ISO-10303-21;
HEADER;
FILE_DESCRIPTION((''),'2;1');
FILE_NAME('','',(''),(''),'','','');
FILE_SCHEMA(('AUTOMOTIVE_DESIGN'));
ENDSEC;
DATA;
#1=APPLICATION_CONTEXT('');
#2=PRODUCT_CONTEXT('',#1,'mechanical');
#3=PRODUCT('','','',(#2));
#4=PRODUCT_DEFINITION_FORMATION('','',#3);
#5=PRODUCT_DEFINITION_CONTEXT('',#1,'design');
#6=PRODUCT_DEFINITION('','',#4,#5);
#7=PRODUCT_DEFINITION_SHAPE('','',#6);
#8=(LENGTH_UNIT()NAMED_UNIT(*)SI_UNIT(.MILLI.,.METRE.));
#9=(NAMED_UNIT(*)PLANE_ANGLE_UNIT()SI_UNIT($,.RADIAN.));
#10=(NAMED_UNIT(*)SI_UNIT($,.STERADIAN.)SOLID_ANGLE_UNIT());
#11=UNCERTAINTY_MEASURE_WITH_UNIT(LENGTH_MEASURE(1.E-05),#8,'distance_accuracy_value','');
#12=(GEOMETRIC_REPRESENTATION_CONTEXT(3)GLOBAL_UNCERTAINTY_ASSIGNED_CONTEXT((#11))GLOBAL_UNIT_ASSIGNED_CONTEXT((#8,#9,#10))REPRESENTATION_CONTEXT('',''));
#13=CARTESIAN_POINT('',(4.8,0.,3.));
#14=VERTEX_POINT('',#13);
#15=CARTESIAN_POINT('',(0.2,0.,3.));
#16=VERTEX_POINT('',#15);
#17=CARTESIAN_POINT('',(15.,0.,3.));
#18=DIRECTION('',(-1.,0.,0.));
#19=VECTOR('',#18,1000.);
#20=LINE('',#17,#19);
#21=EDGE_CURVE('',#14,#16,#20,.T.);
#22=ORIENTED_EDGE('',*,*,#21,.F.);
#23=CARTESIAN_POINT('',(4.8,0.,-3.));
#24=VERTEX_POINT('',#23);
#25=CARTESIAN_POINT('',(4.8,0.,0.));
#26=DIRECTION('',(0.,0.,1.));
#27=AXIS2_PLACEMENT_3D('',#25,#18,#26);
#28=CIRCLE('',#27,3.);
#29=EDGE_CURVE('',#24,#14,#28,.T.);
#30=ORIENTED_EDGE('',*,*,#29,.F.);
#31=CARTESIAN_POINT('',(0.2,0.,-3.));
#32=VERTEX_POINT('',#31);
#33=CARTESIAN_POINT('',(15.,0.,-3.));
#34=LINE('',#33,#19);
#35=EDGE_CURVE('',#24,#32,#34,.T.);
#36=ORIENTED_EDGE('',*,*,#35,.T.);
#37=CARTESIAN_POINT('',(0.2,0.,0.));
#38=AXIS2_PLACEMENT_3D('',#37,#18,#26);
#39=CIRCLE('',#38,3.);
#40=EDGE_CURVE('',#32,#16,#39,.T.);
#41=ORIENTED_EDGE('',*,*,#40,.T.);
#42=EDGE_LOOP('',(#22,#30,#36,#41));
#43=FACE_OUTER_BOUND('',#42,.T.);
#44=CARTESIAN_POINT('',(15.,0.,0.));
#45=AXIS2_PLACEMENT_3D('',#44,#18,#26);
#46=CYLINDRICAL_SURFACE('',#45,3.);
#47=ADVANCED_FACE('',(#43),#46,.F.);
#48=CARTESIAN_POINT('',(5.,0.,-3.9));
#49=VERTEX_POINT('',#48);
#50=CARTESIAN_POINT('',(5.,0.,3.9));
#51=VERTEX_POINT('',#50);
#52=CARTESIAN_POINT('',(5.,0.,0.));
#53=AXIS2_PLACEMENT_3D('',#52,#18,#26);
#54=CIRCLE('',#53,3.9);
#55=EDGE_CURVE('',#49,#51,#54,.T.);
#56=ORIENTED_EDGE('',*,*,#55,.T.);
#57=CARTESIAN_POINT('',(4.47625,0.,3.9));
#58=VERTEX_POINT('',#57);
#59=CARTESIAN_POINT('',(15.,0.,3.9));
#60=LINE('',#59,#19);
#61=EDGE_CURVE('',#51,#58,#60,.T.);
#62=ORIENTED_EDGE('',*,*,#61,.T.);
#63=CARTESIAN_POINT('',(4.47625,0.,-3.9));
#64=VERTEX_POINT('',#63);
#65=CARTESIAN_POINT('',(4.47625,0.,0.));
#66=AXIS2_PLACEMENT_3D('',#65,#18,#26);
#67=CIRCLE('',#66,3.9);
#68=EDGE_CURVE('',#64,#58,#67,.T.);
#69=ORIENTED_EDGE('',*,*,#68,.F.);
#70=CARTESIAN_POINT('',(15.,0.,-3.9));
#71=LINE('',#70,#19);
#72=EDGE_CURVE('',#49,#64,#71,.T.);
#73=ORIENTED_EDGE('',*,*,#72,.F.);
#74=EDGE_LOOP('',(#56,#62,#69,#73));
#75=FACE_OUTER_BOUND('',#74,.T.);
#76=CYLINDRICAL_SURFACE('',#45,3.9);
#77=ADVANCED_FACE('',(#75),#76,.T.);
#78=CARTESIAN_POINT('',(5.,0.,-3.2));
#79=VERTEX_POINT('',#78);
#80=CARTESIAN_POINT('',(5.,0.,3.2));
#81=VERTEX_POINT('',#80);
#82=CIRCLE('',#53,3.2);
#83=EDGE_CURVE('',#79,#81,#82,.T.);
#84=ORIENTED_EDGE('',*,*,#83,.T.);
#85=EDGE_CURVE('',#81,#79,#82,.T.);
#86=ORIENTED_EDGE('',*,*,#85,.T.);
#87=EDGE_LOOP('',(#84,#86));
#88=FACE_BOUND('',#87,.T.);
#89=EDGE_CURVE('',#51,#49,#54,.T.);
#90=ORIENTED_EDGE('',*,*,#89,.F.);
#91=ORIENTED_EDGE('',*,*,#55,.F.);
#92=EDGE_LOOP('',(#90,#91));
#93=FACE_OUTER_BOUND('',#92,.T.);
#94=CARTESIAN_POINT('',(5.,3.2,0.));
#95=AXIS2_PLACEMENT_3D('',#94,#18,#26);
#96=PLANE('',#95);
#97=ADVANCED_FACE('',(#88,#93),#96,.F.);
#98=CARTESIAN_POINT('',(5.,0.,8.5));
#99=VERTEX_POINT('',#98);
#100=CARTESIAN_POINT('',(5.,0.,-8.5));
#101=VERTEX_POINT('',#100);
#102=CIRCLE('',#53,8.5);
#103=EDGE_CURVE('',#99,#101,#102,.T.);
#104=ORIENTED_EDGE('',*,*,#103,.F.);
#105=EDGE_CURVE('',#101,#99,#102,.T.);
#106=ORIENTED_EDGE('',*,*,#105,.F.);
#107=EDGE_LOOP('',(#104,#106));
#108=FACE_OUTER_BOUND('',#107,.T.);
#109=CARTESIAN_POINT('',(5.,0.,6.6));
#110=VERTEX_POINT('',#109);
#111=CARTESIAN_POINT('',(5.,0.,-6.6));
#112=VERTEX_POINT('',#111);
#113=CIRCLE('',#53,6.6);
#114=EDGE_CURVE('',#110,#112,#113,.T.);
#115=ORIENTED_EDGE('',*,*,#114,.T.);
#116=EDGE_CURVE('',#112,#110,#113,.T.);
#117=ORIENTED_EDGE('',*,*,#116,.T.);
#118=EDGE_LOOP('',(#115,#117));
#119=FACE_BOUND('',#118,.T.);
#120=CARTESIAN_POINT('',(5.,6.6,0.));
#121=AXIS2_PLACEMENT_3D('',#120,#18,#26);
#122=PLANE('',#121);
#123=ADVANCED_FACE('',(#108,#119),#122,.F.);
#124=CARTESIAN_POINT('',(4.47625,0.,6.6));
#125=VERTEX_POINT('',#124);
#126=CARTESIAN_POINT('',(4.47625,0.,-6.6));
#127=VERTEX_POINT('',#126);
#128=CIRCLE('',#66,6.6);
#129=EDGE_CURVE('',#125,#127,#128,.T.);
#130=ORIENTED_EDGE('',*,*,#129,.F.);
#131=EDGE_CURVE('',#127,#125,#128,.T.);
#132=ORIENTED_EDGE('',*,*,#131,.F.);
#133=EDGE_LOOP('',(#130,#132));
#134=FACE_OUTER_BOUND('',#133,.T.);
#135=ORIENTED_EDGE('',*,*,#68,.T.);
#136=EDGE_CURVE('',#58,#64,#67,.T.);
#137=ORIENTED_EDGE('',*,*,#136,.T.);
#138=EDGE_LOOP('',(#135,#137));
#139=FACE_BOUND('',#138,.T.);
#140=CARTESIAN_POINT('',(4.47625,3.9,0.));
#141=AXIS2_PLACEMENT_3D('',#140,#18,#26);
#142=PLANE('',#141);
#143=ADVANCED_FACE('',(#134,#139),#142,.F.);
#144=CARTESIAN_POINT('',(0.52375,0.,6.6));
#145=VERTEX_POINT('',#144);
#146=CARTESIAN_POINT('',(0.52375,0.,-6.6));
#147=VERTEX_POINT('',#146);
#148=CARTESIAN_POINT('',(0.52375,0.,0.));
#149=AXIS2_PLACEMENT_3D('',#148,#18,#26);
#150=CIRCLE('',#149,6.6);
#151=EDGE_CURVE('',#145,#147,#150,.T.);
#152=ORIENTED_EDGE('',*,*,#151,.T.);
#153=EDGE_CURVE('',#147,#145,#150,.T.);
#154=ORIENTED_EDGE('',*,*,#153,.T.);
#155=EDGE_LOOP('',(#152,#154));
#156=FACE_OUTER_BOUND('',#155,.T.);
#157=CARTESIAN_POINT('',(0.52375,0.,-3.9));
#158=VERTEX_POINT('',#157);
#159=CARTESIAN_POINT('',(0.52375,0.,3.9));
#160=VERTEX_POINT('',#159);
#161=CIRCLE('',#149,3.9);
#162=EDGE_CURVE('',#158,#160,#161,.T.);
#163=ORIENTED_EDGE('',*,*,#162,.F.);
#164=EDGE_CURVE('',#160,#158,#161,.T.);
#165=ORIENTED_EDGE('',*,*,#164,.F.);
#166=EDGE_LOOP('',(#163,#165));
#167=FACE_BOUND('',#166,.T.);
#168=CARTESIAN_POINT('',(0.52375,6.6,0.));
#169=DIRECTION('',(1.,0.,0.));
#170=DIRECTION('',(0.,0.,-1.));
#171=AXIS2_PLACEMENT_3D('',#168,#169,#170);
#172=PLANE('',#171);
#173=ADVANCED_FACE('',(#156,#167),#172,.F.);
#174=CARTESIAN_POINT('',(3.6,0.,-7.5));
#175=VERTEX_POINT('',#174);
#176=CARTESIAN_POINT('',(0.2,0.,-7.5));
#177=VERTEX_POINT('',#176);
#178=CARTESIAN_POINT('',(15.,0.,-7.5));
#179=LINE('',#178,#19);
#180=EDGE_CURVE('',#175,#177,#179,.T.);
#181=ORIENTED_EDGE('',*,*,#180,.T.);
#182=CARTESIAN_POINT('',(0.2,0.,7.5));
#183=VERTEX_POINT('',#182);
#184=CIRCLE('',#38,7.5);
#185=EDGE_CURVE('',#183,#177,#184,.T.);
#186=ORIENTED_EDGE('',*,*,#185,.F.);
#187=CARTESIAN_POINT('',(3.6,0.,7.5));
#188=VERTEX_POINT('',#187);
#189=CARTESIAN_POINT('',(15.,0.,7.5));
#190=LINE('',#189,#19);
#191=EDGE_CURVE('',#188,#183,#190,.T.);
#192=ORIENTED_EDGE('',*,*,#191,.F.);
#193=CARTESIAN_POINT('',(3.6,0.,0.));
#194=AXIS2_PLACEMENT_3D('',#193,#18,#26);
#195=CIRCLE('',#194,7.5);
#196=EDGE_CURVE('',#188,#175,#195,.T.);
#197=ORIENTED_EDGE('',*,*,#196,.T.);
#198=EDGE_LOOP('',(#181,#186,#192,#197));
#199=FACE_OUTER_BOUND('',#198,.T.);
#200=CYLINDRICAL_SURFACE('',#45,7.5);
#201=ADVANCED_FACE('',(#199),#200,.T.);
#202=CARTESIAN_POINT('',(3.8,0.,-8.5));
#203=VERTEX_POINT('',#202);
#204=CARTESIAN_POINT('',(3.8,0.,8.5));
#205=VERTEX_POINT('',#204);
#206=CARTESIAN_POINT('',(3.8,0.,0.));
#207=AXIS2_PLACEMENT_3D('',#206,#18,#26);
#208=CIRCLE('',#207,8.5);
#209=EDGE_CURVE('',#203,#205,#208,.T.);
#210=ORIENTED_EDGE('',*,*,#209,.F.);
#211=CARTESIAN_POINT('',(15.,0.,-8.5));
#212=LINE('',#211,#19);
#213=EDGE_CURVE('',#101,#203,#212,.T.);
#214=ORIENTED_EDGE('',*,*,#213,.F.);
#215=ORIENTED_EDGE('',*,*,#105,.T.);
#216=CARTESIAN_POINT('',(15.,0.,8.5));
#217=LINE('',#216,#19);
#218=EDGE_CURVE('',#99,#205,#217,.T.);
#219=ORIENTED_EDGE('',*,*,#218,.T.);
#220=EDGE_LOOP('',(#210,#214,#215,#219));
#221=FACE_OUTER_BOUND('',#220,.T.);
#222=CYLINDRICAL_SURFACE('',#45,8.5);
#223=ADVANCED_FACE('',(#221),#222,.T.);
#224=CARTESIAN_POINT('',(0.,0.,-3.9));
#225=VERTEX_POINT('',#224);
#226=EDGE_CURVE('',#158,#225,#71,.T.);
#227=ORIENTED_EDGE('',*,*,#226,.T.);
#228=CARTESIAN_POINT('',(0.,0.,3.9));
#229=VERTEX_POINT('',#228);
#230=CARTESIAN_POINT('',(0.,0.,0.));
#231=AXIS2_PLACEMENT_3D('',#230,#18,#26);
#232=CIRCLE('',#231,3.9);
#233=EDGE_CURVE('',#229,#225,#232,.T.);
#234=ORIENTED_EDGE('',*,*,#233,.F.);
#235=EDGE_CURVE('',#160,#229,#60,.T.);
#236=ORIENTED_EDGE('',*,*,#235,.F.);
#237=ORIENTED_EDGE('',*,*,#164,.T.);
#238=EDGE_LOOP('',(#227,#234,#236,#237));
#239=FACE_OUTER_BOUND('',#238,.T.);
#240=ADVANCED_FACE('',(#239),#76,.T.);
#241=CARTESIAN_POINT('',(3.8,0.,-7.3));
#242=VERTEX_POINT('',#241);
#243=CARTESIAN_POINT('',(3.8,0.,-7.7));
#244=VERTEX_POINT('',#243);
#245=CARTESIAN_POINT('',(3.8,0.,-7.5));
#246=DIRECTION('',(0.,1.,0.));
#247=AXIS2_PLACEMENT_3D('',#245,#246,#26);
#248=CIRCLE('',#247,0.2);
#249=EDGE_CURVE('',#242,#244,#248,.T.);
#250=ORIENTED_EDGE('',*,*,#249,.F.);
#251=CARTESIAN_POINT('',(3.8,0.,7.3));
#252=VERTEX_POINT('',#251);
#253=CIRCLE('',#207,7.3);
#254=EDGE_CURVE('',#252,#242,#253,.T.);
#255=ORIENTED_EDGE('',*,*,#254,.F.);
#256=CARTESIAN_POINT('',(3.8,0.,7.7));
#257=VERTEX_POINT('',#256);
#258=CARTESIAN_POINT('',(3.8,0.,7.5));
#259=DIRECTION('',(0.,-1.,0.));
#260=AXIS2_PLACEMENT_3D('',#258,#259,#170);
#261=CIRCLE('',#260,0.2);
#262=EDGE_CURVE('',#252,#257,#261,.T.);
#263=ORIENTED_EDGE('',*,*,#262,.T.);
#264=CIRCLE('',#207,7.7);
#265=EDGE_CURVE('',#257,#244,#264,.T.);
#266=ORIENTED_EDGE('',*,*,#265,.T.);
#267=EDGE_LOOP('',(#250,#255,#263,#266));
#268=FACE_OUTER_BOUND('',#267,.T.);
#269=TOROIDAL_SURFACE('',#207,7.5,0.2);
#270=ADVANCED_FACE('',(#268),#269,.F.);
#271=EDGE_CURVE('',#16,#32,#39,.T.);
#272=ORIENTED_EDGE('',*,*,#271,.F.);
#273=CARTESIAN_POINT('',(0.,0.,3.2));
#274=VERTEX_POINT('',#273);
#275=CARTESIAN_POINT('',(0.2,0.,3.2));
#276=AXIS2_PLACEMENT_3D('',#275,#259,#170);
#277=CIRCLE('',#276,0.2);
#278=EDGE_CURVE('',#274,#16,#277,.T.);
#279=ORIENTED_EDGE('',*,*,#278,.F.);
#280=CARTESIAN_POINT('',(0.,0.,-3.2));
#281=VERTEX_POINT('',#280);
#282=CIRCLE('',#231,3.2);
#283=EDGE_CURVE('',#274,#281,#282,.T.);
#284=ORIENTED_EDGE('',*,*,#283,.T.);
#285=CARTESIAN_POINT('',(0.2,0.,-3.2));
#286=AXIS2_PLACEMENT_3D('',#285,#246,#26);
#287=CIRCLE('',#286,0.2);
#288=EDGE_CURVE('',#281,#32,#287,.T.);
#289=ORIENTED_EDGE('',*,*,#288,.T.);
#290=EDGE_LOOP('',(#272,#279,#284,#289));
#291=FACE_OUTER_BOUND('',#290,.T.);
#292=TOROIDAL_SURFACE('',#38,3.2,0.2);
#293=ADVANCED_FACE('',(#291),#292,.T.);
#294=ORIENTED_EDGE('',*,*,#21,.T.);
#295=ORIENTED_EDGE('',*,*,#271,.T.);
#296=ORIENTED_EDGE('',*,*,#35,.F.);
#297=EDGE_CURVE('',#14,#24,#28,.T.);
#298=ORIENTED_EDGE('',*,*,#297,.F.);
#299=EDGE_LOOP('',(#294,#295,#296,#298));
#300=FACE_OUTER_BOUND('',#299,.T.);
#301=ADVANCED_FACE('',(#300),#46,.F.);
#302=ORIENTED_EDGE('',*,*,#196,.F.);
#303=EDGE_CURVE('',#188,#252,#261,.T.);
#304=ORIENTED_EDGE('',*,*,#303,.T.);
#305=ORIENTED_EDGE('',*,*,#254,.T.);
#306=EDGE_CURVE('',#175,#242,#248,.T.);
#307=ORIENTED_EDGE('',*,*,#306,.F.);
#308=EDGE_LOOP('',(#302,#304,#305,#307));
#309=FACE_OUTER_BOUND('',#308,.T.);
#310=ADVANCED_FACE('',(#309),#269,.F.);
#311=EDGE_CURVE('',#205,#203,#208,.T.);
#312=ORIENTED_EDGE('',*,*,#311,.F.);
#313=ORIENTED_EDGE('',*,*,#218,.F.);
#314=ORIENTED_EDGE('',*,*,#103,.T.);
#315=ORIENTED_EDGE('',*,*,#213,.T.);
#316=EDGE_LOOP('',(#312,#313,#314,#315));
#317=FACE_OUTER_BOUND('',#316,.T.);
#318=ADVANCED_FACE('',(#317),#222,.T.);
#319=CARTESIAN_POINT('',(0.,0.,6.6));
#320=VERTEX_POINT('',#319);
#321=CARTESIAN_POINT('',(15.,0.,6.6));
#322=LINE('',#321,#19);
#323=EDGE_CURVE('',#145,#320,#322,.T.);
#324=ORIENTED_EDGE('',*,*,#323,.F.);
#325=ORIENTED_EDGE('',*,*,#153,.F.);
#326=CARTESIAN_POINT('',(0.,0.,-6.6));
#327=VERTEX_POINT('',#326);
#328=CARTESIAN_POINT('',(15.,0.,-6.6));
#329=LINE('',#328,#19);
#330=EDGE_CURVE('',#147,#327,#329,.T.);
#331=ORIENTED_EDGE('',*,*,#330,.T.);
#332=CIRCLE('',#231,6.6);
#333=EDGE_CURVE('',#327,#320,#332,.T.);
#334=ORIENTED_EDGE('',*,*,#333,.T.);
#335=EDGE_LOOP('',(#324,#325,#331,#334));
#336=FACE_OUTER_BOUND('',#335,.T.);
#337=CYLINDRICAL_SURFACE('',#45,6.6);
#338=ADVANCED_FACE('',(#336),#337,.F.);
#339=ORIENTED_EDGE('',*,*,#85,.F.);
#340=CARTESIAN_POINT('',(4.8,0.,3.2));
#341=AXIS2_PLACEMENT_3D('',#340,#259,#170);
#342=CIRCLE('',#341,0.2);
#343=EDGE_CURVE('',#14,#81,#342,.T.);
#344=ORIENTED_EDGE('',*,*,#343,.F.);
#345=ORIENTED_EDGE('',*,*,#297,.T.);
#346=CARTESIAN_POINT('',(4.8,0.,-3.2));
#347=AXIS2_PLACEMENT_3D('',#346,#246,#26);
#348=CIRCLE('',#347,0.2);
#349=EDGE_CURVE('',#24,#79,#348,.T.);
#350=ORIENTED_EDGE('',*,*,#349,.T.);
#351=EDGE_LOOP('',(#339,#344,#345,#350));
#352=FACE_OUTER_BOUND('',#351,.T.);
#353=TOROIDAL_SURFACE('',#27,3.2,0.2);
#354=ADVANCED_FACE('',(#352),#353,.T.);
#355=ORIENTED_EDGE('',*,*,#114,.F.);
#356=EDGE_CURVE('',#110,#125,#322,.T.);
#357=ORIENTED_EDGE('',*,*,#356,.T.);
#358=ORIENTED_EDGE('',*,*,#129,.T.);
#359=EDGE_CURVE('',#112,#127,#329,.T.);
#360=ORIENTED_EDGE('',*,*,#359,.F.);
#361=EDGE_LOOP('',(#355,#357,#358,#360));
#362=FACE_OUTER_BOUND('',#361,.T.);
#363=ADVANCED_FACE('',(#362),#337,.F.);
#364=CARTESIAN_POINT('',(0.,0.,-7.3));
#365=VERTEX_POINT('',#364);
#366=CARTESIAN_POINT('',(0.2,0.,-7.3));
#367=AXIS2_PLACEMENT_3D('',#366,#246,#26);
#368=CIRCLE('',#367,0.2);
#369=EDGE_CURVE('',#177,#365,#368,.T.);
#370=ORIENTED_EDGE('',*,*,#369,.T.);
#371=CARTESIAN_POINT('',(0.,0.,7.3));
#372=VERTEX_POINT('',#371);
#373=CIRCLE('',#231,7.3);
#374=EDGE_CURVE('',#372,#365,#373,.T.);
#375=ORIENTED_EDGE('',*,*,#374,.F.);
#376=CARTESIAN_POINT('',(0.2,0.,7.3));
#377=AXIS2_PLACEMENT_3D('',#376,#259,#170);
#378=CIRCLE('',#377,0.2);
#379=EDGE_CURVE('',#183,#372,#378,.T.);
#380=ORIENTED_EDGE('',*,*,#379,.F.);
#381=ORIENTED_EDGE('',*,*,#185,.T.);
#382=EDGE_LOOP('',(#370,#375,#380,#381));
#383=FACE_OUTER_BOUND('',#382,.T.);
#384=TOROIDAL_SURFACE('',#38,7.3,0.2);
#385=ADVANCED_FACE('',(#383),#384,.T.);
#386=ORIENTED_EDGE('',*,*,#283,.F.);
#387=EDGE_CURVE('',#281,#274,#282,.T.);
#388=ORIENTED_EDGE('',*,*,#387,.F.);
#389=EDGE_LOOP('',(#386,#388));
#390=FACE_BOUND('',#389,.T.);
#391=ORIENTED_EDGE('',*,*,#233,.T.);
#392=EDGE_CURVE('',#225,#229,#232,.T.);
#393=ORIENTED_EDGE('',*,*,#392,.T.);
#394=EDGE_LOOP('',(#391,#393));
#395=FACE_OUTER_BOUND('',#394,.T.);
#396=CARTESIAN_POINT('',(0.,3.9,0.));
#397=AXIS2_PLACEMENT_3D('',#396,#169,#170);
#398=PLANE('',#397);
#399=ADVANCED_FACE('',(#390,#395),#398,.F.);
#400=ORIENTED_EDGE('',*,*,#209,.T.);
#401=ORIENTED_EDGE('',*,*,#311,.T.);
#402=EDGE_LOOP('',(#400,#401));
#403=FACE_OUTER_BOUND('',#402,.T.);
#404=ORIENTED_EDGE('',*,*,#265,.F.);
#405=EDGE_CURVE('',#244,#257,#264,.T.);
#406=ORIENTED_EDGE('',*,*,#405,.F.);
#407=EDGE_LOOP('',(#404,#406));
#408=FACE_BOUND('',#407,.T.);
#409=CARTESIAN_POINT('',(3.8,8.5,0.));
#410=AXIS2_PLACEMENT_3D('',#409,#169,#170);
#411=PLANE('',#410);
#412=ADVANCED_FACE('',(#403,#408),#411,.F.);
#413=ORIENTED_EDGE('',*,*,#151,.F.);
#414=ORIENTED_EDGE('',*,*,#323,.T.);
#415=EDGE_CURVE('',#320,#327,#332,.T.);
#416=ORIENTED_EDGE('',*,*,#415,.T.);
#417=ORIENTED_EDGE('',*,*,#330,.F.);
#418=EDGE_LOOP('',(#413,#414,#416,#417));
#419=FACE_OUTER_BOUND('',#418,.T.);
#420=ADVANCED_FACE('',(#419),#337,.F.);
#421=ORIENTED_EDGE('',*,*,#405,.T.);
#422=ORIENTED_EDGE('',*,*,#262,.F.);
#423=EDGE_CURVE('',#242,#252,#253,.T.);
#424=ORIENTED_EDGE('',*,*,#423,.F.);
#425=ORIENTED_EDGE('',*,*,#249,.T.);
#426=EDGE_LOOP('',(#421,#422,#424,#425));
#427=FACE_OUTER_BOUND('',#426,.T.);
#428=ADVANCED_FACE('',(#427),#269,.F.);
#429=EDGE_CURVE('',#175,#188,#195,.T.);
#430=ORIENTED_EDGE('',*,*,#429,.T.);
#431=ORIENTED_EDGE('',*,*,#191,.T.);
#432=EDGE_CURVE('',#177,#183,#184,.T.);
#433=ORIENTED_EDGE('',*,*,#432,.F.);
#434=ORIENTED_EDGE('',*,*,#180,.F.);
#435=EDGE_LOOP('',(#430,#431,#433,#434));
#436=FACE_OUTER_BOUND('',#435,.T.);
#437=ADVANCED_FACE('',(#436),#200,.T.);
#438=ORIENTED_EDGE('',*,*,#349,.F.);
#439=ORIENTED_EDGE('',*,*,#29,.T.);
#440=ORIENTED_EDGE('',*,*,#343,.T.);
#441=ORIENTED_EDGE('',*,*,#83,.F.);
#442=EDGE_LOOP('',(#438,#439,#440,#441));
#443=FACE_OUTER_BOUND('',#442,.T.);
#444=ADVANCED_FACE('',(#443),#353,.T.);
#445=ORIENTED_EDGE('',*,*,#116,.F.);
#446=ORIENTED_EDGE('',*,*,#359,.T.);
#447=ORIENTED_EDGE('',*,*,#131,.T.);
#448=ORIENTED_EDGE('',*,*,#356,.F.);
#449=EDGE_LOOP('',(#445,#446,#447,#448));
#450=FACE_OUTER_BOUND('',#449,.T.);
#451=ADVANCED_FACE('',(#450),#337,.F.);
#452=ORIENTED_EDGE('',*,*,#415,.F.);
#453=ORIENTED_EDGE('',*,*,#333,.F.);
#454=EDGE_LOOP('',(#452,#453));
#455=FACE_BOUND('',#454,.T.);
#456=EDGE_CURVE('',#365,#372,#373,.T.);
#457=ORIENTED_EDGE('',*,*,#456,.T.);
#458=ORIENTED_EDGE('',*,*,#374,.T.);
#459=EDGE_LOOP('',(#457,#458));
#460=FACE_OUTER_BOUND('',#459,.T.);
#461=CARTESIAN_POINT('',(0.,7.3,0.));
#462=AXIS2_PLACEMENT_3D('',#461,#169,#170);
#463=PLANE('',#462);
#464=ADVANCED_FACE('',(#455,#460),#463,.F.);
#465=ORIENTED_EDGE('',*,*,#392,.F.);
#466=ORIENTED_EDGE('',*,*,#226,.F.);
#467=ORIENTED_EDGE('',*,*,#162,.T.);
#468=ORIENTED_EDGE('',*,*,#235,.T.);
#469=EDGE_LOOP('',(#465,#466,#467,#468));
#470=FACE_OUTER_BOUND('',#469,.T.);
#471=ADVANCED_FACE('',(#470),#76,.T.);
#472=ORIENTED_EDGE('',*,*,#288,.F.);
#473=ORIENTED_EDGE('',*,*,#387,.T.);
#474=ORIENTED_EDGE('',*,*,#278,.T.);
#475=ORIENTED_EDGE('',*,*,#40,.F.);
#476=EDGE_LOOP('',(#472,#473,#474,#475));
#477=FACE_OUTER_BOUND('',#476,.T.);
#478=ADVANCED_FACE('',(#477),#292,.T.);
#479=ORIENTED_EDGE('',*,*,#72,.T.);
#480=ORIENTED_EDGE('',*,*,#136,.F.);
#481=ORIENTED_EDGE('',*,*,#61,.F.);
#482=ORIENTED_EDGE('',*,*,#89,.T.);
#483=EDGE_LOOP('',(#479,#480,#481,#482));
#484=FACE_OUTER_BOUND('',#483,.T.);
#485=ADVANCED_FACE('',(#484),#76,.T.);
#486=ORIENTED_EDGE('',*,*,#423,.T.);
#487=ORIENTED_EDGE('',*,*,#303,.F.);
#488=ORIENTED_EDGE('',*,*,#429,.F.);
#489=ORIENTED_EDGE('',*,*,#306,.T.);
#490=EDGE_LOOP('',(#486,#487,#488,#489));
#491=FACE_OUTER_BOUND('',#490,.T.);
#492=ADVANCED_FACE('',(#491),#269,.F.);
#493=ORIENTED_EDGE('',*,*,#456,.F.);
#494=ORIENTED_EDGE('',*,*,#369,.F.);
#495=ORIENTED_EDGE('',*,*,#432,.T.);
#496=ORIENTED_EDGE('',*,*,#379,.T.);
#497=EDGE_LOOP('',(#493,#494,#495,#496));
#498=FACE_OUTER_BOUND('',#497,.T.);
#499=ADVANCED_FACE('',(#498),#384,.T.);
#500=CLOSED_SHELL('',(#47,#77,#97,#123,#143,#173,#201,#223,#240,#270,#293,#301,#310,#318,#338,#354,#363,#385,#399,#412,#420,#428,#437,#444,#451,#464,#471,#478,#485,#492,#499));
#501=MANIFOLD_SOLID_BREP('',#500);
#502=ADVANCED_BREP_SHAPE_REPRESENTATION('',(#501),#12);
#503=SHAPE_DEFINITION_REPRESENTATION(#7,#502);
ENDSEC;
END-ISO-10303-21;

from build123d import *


with BuildPart() as part:
    # Sketch1 → Revolve1 (revolve)
    with BuildSketch(Plane.XY, mode=Mode.PRIVATE) as revolve1_sk:
        with BuildLine():
            Line((0, 7.3), (0, 6.6))
            Line((0, 6.6), (0.52375, 6.6))
            Line((0.52375, 6.6), (0.52375, 3.9))
            Line((0.52375, 3.9), (0, 3.9))
            Line((0, 3.9), (0, 3.2))
            ThreePointArc((0, 3.2), (0.058578644, 3.058578644), (0.2, 3))
            Line((0.2, 3), (4.8, 3))
            ThreePointArc((4.8, 3), (4.941421356, 3.058578644), (5, 3.2))
            Line((5, 3.2), (5, 3.9))
            Line((5, 3.9), (4.47625, 3.9))
            Line((4.47625, 3.9), (4.47625, 6.6))
            Line((4.47625, 6.6), (5, 6.6))
            Line((5, 6.6), (5, 8.5))
            Line((5, 8.5), (3.8, 8.5))
            Line((3.8, 8.5), (3.8, 7.7))
            ThreePointArc((3.8, 7.7), (3.941421356, 7.358578644), (3.6, 7.5))
            Line((3.6, 7.5), (0.2, 7.5))
            ThreePointArc((0.2, 7.5), (0.058578644, 7.441421356), (0, 7.3))
        make_face()
    revolve(revolve1_sk.sketch.rotate(Axis((15, 0, 0), (-1, 0, 0)), 270), axis=Axis((15, 0, 0), (-1, 0, 0)))


solid = part.part
